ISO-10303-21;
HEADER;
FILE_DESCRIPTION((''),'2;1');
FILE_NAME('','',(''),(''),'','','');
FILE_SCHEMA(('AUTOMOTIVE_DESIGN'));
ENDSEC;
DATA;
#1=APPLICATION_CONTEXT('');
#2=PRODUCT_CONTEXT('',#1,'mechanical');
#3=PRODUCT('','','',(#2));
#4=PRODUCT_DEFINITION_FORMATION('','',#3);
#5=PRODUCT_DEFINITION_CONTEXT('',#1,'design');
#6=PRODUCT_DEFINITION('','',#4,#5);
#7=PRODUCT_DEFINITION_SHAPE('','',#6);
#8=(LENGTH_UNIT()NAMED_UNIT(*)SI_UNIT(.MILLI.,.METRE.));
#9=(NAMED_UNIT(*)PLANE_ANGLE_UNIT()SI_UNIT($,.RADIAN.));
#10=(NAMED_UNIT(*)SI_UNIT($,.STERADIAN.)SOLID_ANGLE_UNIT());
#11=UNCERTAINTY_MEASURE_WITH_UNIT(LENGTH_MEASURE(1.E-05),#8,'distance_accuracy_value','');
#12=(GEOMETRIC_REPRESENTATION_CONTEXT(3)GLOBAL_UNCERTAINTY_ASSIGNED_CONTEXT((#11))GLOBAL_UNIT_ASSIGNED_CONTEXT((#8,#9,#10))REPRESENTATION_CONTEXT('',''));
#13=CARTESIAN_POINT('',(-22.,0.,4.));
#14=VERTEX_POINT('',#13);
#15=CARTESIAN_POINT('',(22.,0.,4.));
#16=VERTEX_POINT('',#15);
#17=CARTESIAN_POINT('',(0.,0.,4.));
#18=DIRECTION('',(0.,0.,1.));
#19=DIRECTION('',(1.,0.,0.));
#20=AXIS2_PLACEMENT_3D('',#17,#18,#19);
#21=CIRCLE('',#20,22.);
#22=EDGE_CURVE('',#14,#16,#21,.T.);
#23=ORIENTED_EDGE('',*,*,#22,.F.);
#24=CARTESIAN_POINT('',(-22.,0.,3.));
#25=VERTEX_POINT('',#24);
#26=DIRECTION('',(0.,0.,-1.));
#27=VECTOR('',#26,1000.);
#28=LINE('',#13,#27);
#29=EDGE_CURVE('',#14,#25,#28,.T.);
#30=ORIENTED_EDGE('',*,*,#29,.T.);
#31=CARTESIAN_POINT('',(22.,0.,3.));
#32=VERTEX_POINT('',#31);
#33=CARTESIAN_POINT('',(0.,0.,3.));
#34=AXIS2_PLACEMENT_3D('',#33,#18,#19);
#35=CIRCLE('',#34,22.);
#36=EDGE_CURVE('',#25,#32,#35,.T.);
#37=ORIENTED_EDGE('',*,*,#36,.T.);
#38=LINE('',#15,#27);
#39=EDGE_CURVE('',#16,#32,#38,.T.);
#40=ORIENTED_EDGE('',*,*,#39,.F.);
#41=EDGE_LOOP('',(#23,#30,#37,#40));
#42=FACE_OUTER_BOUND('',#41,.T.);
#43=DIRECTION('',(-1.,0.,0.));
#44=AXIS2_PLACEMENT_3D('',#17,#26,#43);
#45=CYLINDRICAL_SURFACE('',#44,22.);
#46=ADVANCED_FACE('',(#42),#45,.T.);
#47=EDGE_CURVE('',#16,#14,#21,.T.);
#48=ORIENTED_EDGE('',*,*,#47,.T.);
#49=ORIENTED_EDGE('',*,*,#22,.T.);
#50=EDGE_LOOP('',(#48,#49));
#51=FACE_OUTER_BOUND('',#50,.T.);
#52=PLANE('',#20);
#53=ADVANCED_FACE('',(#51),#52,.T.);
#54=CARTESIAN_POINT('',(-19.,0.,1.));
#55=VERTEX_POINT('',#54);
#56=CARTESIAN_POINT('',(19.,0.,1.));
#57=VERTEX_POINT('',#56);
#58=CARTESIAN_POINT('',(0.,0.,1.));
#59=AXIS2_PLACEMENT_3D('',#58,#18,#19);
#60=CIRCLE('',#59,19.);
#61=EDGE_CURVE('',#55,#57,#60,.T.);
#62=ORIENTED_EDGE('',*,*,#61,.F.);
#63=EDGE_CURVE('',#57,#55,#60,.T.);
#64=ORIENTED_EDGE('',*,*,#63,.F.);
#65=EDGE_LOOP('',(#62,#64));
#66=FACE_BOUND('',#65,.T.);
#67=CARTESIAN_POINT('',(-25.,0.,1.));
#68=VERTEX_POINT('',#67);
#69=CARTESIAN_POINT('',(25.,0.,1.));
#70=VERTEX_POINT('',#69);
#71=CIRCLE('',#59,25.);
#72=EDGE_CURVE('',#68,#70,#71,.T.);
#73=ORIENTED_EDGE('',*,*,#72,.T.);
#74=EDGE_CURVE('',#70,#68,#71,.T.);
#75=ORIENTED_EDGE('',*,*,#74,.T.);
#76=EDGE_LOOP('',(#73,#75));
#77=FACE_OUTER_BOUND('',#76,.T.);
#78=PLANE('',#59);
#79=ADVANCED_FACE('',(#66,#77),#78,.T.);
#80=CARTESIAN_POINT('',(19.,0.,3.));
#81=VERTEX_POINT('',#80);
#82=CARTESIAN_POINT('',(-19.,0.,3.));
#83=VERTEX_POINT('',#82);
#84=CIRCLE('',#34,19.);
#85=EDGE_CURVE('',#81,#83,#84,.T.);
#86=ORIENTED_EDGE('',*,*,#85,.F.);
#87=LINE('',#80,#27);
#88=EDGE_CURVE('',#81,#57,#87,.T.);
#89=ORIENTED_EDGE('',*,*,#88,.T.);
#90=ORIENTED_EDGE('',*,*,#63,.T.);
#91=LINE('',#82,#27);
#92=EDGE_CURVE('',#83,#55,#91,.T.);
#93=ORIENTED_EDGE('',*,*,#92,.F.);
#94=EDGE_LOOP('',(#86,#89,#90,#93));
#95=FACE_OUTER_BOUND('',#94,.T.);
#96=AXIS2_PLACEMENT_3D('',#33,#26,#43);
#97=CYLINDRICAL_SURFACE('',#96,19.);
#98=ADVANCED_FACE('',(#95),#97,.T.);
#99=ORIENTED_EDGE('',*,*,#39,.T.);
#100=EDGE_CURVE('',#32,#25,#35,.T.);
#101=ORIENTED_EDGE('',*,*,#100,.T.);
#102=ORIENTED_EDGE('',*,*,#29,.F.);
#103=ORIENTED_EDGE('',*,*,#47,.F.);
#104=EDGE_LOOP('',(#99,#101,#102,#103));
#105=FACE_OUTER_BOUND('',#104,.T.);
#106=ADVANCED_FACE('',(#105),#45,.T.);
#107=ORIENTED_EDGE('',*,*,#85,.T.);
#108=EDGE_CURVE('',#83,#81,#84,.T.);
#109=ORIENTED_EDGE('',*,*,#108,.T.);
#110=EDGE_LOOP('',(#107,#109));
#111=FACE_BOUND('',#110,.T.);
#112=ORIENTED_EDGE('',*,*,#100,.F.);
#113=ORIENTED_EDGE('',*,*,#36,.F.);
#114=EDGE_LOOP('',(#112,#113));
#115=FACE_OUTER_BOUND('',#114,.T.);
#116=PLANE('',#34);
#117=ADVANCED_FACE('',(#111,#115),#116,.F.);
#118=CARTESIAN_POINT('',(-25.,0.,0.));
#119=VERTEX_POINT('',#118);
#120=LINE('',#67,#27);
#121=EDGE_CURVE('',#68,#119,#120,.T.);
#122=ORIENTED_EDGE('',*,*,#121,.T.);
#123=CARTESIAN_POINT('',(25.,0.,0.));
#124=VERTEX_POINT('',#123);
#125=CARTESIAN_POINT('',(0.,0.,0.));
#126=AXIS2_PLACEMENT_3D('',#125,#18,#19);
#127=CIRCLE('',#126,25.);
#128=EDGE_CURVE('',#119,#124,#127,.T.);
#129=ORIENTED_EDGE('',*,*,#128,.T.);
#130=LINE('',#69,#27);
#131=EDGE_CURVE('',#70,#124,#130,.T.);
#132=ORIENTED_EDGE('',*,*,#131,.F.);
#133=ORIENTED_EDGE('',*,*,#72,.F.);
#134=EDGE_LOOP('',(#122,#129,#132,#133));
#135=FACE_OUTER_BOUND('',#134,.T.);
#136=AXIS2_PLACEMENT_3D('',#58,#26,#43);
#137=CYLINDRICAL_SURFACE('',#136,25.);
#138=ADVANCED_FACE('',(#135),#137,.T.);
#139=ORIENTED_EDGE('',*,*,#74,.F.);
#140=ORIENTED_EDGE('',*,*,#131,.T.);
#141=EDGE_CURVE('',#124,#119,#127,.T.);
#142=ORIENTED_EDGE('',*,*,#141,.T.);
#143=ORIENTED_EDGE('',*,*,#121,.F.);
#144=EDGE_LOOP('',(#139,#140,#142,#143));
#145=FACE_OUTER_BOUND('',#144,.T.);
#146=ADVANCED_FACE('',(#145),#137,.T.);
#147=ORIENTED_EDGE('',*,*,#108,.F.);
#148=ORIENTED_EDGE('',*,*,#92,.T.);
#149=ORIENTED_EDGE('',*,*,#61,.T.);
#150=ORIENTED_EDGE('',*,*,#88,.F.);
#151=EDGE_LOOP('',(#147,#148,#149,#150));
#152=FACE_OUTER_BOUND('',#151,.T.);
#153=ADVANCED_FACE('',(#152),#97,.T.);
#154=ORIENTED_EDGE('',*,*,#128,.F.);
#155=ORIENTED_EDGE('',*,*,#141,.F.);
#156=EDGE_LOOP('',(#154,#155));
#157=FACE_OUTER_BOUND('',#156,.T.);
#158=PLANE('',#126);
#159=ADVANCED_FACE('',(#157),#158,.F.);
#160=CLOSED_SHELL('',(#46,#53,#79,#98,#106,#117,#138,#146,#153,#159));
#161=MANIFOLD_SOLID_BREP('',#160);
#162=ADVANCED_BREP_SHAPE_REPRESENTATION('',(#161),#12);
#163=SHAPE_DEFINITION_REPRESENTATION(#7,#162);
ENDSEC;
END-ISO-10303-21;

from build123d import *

# Parameters (mm, degrees)
SKETCH_3_R           = 25
BOSS_EXTRUDE_1_DEPTH = 1
SKETCH_4_R           = 19
BOSS_EXTRUDE_2_DEPTH = 2
SKETCH_5_R           = 22
BOSS_EXTRUDE_3_DEPTH = 1


with BuildPart() as part:
    # Sketch 3 → Boss-Extrude 1 (new body)
    with BuildSketch(Plane.XY):
        Circle(SKETCH_3_R)
    extrude(amount=BOSS_EXTRUDE_1_DEPTH)

    # Sketch 4 → Boss-Extrude 2 (add)
    with BuildSketch(Plane.XY.offset(1)):
        Circle(SKETCH_4_R)
    extrude(amount=BOSS_EXTRUDE_2_DEPTH)

    # Sketch 5 → Boss-Extrude 3 (add)
    with BuildSketch(Plane.XY.offset(3)):
        Circle(SKETCH_5_R)
    extrude(amount=BOSS_EXTRUDE_3_DEPTH)


solid = part.part
